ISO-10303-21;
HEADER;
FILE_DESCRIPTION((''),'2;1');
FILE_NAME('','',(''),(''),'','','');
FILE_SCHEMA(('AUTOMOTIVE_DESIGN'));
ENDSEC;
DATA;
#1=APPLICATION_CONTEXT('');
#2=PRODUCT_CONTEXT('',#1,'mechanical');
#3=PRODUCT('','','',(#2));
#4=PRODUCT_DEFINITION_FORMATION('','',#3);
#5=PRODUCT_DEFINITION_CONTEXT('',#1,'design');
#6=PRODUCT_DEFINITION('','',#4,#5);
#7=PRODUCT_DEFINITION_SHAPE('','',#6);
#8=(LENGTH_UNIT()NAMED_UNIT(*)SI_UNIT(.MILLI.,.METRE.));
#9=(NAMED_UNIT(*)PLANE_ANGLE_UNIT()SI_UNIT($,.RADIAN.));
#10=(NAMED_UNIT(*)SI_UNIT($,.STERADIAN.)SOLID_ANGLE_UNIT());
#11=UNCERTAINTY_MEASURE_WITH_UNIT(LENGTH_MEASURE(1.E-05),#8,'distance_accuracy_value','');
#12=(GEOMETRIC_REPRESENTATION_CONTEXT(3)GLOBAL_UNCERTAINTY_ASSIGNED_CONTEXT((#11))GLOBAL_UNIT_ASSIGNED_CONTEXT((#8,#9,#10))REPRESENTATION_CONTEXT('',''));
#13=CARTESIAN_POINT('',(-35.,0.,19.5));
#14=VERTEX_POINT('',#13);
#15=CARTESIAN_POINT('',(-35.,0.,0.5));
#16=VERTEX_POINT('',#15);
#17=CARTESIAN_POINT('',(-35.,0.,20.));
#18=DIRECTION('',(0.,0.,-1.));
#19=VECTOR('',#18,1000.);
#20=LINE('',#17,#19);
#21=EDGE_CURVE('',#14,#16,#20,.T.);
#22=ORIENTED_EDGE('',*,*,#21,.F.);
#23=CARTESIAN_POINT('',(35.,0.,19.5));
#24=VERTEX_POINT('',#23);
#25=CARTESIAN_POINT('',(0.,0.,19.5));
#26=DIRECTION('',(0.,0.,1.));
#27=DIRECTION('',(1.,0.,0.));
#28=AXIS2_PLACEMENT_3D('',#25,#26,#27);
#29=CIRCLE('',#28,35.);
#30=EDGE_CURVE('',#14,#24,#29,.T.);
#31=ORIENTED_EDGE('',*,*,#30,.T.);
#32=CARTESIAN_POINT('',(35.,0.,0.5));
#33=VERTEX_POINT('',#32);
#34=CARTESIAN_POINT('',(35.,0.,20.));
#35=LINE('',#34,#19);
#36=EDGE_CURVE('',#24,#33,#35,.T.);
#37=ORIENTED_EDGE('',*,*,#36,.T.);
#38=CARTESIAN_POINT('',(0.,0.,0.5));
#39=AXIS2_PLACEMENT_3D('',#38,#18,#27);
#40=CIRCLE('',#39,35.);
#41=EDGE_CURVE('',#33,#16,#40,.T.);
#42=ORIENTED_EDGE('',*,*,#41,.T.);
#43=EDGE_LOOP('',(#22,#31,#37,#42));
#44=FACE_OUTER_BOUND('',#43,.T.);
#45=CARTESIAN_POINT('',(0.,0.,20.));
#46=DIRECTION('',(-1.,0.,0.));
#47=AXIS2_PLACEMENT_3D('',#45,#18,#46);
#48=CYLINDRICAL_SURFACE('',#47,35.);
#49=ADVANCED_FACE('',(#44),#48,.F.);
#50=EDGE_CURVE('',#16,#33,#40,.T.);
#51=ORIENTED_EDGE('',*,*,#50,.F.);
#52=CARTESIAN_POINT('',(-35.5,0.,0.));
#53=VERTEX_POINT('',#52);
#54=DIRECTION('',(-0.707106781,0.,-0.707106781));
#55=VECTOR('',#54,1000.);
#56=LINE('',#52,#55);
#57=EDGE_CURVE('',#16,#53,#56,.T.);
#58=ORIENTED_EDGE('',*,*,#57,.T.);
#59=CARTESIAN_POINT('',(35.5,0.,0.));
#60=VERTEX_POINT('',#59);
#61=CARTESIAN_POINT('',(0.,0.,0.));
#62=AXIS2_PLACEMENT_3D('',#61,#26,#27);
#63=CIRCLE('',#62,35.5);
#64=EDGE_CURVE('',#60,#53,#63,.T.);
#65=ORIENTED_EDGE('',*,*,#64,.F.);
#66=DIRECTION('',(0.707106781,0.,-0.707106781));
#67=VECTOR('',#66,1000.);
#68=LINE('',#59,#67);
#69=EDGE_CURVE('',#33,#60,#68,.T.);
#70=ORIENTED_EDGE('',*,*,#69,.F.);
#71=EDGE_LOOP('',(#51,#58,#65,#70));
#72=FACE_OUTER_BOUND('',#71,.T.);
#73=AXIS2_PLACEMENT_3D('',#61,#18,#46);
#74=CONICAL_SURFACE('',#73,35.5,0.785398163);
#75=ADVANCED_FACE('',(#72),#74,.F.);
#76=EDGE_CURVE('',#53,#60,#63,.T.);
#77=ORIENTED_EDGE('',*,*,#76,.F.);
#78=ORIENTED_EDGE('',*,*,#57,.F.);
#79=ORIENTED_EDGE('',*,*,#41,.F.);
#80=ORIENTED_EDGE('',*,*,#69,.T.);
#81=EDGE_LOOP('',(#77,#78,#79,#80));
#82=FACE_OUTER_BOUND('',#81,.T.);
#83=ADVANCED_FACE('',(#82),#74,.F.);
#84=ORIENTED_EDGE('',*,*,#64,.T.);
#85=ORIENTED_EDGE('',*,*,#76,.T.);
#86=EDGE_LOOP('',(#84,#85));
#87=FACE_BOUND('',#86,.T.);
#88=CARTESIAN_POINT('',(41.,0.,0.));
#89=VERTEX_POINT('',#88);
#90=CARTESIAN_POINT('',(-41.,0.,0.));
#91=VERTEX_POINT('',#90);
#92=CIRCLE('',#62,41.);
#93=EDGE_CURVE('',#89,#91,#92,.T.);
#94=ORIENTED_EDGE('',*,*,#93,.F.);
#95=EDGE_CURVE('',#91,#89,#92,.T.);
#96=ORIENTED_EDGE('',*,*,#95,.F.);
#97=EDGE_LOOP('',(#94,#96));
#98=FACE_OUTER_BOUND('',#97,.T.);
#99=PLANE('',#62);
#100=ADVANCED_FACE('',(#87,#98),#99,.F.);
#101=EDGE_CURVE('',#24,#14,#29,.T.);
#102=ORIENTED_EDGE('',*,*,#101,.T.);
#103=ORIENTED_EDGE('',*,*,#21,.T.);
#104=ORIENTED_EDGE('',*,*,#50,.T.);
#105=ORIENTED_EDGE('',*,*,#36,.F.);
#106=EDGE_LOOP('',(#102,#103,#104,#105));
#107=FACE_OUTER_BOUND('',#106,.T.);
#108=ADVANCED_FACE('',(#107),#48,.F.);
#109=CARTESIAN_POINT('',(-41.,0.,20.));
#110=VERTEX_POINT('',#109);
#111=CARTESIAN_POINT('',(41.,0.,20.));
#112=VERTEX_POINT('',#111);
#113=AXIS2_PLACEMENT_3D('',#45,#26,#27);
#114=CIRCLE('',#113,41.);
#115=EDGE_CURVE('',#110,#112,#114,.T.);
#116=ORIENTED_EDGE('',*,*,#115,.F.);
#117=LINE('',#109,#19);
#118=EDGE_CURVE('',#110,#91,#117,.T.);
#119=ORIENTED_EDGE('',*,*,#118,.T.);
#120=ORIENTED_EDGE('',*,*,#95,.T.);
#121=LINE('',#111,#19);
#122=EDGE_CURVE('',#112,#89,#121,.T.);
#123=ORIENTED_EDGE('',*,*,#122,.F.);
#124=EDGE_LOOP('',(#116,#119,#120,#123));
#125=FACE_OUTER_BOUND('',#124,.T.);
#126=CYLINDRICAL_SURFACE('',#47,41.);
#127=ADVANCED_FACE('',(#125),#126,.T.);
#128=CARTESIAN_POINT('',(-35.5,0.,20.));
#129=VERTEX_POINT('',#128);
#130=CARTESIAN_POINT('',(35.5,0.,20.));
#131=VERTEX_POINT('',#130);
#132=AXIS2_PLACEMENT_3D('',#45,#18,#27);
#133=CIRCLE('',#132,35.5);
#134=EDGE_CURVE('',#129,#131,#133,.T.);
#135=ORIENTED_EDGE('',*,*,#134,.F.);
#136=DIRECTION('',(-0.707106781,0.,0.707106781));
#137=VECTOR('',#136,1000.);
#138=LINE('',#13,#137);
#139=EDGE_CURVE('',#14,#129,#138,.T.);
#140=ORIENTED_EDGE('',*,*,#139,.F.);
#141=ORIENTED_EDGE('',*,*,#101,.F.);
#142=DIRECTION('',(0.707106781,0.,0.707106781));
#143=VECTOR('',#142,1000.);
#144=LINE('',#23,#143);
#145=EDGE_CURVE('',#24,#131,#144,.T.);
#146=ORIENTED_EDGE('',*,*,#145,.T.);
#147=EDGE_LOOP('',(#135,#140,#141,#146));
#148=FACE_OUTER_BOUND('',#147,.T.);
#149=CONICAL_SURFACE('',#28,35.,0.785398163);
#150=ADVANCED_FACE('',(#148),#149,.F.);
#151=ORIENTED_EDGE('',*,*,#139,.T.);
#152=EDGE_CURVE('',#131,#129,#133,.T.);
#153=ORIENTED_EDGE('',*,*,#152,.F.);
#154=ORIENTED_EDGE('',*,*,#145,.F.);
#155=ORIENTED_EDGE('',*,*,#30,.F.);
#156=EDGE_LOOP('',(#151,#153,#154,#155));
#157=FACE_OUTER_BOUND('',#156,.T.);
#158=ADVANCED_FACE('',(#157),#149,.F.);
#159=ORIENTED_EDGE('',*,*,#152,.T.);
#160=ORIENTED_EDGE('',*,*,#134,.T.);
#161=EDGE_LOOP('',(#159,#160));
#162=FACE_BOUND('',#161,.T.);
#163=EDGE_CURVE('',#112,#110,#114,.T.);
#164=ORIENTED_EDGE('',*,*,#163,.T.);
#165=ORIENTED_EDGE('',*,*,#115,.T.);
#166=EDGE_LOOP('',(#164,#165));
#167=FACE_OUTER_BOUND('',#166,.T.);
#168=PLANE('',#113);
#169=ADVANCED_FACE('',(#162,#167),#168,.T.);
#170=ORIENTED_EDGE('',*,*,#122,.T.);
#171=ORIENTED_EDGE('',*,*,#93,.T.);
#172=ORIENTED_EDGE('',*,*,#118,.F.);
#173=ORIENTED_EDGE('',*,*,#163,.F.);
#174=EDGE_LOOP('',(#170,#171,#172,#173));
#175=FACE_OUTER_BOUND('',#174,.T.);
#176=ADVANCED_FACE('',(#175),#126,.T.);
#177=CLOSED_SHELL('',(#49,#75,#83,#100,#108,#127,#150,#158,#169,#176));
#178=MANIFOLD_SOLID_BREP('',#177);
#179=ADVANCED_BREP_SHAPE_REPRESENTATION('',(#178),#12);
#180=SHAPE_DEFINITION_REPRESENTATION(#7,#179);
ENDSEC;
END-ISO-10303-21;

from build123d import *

# Parameters (mm, degrees)
SKETCH1_R           = 41
SKETCH1_R_2         = 35
BOSS_EXTRUDE1_DEPTH = 20
CHAMFER1_SIZE       = 0.5


with BuildPart() as part:
    # Sketch1 → Boss-Extrude1 (new body)
    with BuildSketch(Plane.XY):
        Circle(SKETCH1_R)
        Circle(SKETCH1_R_2, mode=Mode.SUBTRACT)
    extrude(amount=BOSS_EXTRUDE1_DEPTH)

    # Chamfer1
    chamfer1_edges = [part.edges().sort_by_distance(p)[0] for p in [
        (-35, 0, 0),
        (-35, 0, 20),
    ]]
    chamfer(chamfer1_edges, length=CHAMFER1_SIZE)


solid = part.part
